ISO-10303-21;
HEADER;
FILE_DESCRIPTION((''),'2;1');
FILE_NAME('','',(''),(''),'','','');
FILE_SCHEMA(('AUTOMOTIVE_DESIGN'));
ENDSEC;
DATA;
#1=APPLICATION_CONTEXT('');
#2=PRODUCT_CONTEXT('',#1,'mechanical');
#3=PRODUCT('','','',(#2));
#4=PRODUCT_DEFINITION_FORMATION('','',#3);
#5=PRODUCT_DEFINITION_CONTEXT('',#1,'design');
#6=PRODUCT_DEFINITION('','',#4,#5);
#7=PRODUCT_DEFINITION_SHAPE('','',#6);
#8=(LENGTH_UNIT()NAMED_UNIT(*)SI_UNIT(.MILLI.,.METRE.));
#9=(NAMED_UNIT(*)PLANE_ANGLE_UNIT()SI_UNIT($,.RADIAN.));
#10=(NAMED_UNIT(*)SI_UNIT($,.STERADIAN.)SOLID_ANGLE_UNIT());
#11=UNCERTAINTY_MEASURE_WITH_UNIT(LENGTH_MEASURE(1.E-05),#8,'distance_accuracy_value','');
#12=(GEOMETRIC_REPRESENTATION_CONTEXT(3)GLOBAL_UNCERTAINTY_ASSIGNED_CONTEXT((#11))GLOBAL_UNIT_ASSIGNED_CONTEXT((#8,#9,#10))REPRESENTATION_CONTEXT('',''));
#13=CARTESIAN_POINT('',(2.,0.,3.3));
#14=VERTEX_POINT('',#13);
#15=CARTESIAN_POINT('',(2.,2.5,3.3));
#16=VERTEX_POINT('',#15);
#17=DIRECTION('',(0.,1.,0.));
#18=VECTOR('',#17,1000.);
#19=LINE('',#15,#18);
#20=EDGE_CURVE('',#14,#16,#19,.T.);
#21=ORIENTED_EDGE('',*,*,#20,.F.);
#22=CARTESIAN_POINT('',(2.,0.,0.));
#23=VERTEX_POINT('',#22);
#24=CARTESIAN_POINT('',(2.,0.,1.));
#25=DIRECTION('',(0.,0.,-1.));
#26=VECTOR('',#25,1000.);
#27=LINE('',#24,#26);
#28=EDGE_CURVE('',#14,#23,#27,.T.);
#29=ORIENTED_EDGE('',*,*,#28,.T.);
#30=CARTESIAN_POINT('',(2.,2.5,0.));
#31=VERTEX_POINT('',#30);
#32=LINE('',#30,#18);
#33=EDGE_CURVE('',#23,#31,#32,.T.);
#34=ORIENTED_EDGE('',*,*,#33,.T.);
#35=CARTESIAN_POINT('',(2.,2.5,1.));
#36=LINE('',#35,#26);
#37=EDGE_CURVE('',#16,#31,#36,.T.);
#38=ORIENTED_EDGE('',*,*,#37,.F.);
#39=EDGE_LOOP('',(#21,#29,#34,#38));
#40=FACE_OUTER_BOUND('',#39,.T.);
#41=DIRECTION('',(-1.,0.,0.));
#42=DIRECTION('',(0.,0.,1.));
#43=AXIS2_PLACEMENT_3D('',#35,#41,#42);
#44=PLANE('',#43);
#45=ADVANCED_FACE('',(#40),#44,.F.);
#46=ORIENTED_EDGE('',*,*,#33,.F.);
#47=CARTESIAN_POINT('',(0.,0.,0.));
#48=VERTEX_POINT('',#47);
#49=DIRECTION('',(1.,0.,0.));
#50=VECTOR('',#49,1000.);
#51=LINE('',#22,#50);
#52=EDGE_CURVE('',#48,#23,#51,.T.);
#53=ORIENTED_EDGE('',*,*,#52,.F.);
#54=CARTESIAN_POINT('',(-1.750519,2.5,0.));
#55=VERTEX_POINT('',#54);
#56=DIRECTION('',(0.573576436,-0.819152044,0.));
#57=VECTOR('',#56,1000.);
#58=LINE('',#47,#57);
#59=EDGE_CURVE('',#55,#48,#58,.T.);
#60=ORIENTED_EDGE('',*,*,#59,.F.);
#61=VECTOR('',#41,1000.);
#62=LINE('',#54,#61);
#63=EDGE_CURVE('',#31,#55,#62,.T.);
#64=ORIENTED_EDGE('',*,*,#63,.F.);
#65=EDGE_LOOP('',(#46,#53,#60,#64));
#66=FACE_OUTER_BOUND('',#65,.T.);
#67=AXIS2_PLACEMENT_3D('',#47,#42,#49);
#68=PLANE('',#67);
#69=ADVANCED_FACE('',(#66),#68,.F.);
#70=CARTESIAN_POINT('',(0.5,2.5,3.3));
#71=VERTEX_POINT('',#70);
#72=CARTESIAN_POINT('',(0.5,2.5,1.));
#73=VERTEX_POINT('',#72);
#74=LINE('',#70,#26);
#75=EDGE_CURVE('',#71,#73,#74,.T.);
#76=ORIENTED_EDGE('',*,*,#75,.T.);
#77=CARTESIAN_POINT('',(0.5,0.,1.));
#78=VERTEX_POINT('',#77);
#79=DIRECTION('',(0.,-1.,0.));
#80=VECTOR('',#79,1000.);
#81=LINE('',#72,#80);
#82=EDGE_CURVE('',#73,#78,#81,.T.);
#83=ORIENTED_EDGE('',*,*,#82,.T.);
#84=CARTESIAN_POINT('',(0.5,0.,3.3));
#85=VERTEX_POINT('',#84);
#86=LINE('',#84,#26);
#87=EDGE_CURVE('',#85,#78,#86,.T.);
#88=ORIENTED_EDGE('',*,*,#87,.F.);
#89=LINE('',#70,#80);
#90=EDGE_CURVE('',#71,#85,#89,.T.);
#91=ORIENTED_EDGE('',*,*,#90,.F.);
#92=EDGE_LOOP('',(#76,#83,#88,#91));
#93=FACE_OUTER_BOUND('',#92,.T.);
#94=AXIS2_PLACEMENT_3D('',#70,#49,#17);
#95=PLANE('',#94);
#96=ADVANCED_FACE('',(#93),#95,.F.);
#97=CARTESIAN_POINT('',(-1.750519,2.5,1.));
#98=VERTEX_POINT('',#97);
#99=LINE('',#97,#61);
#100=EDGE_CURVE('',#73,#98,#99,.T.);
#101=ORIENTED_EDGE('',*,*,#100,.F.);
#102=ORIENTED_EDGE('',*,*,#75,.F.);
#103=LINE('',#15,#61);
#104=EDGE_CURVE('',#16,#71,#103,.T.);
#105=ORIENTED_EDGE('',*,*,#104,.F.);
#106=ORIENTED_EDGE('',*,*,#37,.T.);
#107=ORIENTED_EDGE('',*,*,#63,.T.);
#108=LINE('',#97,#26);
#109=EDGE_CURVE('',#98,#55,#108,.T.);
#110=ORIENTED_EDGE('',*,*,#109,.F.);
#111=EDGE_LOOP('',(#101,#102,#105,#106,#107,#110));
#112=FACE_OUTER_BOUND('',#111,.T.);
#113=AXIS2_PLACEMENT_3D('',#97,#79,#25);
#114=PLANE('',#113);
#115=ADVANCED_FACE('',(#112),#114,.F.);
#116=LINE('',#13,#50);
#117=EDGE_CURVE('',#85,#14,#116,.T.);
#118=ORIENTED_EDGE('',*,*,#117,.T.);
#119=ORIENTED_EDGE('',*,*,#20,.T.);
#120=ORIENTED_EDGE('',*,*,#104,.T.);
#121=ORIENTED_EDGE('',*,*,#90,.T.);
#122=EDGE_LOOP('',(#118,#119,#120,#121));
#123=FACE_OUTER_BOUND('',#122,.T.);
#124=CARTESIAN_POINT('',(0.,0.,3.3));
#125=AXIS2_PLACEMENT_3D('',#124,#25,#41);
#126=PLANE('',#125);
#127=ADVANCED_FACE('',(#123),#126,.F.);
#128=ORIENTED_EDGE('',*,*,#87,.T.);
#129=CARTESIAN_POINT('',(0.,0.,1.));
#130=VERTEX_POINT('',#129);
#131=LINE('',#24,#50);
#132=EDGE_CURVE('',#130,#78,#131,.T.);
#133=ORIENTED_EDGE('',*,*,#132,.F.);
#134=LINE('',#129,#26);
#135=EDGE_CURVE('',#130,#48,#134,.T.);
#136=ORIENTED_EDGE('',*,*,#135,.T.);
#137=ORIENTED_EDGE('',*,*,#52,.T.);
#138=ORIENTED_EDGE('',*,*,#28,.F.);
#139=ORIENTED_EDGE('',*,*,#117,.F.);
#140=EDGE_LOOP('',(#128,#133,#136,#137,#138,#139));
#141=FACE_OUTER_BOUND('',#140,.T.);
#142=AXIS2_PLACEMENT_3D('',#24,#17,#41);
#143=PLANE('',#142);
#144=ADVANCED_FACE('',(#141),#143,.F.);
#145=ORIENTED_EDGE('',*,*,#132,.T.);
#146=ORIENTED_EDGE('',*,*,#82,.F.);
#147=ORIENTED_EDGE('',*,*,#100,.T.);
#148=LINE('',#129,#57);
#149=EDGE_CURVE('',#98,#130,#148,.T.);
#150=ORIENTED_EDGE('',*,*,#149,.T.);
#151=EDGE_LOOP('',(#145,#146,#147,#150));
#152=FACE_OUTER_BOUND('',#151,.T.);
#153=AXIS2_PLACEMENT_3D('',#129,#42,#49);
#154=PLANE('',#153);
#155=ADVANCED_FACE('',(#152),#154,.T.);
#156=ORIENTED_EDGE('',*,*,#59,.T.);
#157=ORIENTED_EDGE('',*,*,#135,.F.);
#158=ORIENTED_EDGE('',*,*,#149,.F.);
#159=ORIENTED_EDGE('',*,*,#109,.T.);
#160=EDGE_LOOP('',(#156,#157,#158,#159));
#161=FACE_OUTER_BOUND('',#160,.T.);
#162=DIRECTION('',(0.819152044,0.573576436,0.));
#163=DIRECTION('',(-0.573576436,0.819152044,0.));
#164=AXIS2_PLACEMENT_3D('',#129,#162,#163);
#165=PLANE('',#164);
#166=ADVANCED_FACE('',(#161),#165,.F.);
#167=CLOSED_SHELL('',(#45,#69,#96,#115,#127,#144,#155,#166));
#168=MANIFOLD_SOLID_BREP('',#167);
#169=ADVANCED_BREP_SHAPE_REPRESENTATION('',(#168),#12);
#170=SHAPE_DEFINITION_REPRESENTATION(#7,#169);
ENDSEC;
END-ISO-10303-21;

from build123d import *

# Parameters (mm, degrees)
BOSS_EXTRUDE1_DEPTH = 1
SKETCH2_W           = 1.5
SKETCH2_H           = 2.5
BOSS_EXTRUDE2_DEPTH = 2.3


with BuildPart() as part:
    # Sketch1 → Boss-Extrude1 (new body)
    with BuildSketch(Plane.XY):
        Polygon((0, 0), (-1.750518846, 2.5), (2, 2.5), (2, 0), align=None)
    extrude(amount=BOSS_EXTRUDE1_DEPTH)

    # Sketch2 → Boss-Extrude2 (add)
    with BuildSketch(Plane.XY.offset(1)):
        with Locations((1.25, 1.25)):
            Rectangle(SKETCH2_W, SKETCH2_H)
    extrude(amount=BOSS_EXTRUDE2_DEPTH)


solid = part.part
